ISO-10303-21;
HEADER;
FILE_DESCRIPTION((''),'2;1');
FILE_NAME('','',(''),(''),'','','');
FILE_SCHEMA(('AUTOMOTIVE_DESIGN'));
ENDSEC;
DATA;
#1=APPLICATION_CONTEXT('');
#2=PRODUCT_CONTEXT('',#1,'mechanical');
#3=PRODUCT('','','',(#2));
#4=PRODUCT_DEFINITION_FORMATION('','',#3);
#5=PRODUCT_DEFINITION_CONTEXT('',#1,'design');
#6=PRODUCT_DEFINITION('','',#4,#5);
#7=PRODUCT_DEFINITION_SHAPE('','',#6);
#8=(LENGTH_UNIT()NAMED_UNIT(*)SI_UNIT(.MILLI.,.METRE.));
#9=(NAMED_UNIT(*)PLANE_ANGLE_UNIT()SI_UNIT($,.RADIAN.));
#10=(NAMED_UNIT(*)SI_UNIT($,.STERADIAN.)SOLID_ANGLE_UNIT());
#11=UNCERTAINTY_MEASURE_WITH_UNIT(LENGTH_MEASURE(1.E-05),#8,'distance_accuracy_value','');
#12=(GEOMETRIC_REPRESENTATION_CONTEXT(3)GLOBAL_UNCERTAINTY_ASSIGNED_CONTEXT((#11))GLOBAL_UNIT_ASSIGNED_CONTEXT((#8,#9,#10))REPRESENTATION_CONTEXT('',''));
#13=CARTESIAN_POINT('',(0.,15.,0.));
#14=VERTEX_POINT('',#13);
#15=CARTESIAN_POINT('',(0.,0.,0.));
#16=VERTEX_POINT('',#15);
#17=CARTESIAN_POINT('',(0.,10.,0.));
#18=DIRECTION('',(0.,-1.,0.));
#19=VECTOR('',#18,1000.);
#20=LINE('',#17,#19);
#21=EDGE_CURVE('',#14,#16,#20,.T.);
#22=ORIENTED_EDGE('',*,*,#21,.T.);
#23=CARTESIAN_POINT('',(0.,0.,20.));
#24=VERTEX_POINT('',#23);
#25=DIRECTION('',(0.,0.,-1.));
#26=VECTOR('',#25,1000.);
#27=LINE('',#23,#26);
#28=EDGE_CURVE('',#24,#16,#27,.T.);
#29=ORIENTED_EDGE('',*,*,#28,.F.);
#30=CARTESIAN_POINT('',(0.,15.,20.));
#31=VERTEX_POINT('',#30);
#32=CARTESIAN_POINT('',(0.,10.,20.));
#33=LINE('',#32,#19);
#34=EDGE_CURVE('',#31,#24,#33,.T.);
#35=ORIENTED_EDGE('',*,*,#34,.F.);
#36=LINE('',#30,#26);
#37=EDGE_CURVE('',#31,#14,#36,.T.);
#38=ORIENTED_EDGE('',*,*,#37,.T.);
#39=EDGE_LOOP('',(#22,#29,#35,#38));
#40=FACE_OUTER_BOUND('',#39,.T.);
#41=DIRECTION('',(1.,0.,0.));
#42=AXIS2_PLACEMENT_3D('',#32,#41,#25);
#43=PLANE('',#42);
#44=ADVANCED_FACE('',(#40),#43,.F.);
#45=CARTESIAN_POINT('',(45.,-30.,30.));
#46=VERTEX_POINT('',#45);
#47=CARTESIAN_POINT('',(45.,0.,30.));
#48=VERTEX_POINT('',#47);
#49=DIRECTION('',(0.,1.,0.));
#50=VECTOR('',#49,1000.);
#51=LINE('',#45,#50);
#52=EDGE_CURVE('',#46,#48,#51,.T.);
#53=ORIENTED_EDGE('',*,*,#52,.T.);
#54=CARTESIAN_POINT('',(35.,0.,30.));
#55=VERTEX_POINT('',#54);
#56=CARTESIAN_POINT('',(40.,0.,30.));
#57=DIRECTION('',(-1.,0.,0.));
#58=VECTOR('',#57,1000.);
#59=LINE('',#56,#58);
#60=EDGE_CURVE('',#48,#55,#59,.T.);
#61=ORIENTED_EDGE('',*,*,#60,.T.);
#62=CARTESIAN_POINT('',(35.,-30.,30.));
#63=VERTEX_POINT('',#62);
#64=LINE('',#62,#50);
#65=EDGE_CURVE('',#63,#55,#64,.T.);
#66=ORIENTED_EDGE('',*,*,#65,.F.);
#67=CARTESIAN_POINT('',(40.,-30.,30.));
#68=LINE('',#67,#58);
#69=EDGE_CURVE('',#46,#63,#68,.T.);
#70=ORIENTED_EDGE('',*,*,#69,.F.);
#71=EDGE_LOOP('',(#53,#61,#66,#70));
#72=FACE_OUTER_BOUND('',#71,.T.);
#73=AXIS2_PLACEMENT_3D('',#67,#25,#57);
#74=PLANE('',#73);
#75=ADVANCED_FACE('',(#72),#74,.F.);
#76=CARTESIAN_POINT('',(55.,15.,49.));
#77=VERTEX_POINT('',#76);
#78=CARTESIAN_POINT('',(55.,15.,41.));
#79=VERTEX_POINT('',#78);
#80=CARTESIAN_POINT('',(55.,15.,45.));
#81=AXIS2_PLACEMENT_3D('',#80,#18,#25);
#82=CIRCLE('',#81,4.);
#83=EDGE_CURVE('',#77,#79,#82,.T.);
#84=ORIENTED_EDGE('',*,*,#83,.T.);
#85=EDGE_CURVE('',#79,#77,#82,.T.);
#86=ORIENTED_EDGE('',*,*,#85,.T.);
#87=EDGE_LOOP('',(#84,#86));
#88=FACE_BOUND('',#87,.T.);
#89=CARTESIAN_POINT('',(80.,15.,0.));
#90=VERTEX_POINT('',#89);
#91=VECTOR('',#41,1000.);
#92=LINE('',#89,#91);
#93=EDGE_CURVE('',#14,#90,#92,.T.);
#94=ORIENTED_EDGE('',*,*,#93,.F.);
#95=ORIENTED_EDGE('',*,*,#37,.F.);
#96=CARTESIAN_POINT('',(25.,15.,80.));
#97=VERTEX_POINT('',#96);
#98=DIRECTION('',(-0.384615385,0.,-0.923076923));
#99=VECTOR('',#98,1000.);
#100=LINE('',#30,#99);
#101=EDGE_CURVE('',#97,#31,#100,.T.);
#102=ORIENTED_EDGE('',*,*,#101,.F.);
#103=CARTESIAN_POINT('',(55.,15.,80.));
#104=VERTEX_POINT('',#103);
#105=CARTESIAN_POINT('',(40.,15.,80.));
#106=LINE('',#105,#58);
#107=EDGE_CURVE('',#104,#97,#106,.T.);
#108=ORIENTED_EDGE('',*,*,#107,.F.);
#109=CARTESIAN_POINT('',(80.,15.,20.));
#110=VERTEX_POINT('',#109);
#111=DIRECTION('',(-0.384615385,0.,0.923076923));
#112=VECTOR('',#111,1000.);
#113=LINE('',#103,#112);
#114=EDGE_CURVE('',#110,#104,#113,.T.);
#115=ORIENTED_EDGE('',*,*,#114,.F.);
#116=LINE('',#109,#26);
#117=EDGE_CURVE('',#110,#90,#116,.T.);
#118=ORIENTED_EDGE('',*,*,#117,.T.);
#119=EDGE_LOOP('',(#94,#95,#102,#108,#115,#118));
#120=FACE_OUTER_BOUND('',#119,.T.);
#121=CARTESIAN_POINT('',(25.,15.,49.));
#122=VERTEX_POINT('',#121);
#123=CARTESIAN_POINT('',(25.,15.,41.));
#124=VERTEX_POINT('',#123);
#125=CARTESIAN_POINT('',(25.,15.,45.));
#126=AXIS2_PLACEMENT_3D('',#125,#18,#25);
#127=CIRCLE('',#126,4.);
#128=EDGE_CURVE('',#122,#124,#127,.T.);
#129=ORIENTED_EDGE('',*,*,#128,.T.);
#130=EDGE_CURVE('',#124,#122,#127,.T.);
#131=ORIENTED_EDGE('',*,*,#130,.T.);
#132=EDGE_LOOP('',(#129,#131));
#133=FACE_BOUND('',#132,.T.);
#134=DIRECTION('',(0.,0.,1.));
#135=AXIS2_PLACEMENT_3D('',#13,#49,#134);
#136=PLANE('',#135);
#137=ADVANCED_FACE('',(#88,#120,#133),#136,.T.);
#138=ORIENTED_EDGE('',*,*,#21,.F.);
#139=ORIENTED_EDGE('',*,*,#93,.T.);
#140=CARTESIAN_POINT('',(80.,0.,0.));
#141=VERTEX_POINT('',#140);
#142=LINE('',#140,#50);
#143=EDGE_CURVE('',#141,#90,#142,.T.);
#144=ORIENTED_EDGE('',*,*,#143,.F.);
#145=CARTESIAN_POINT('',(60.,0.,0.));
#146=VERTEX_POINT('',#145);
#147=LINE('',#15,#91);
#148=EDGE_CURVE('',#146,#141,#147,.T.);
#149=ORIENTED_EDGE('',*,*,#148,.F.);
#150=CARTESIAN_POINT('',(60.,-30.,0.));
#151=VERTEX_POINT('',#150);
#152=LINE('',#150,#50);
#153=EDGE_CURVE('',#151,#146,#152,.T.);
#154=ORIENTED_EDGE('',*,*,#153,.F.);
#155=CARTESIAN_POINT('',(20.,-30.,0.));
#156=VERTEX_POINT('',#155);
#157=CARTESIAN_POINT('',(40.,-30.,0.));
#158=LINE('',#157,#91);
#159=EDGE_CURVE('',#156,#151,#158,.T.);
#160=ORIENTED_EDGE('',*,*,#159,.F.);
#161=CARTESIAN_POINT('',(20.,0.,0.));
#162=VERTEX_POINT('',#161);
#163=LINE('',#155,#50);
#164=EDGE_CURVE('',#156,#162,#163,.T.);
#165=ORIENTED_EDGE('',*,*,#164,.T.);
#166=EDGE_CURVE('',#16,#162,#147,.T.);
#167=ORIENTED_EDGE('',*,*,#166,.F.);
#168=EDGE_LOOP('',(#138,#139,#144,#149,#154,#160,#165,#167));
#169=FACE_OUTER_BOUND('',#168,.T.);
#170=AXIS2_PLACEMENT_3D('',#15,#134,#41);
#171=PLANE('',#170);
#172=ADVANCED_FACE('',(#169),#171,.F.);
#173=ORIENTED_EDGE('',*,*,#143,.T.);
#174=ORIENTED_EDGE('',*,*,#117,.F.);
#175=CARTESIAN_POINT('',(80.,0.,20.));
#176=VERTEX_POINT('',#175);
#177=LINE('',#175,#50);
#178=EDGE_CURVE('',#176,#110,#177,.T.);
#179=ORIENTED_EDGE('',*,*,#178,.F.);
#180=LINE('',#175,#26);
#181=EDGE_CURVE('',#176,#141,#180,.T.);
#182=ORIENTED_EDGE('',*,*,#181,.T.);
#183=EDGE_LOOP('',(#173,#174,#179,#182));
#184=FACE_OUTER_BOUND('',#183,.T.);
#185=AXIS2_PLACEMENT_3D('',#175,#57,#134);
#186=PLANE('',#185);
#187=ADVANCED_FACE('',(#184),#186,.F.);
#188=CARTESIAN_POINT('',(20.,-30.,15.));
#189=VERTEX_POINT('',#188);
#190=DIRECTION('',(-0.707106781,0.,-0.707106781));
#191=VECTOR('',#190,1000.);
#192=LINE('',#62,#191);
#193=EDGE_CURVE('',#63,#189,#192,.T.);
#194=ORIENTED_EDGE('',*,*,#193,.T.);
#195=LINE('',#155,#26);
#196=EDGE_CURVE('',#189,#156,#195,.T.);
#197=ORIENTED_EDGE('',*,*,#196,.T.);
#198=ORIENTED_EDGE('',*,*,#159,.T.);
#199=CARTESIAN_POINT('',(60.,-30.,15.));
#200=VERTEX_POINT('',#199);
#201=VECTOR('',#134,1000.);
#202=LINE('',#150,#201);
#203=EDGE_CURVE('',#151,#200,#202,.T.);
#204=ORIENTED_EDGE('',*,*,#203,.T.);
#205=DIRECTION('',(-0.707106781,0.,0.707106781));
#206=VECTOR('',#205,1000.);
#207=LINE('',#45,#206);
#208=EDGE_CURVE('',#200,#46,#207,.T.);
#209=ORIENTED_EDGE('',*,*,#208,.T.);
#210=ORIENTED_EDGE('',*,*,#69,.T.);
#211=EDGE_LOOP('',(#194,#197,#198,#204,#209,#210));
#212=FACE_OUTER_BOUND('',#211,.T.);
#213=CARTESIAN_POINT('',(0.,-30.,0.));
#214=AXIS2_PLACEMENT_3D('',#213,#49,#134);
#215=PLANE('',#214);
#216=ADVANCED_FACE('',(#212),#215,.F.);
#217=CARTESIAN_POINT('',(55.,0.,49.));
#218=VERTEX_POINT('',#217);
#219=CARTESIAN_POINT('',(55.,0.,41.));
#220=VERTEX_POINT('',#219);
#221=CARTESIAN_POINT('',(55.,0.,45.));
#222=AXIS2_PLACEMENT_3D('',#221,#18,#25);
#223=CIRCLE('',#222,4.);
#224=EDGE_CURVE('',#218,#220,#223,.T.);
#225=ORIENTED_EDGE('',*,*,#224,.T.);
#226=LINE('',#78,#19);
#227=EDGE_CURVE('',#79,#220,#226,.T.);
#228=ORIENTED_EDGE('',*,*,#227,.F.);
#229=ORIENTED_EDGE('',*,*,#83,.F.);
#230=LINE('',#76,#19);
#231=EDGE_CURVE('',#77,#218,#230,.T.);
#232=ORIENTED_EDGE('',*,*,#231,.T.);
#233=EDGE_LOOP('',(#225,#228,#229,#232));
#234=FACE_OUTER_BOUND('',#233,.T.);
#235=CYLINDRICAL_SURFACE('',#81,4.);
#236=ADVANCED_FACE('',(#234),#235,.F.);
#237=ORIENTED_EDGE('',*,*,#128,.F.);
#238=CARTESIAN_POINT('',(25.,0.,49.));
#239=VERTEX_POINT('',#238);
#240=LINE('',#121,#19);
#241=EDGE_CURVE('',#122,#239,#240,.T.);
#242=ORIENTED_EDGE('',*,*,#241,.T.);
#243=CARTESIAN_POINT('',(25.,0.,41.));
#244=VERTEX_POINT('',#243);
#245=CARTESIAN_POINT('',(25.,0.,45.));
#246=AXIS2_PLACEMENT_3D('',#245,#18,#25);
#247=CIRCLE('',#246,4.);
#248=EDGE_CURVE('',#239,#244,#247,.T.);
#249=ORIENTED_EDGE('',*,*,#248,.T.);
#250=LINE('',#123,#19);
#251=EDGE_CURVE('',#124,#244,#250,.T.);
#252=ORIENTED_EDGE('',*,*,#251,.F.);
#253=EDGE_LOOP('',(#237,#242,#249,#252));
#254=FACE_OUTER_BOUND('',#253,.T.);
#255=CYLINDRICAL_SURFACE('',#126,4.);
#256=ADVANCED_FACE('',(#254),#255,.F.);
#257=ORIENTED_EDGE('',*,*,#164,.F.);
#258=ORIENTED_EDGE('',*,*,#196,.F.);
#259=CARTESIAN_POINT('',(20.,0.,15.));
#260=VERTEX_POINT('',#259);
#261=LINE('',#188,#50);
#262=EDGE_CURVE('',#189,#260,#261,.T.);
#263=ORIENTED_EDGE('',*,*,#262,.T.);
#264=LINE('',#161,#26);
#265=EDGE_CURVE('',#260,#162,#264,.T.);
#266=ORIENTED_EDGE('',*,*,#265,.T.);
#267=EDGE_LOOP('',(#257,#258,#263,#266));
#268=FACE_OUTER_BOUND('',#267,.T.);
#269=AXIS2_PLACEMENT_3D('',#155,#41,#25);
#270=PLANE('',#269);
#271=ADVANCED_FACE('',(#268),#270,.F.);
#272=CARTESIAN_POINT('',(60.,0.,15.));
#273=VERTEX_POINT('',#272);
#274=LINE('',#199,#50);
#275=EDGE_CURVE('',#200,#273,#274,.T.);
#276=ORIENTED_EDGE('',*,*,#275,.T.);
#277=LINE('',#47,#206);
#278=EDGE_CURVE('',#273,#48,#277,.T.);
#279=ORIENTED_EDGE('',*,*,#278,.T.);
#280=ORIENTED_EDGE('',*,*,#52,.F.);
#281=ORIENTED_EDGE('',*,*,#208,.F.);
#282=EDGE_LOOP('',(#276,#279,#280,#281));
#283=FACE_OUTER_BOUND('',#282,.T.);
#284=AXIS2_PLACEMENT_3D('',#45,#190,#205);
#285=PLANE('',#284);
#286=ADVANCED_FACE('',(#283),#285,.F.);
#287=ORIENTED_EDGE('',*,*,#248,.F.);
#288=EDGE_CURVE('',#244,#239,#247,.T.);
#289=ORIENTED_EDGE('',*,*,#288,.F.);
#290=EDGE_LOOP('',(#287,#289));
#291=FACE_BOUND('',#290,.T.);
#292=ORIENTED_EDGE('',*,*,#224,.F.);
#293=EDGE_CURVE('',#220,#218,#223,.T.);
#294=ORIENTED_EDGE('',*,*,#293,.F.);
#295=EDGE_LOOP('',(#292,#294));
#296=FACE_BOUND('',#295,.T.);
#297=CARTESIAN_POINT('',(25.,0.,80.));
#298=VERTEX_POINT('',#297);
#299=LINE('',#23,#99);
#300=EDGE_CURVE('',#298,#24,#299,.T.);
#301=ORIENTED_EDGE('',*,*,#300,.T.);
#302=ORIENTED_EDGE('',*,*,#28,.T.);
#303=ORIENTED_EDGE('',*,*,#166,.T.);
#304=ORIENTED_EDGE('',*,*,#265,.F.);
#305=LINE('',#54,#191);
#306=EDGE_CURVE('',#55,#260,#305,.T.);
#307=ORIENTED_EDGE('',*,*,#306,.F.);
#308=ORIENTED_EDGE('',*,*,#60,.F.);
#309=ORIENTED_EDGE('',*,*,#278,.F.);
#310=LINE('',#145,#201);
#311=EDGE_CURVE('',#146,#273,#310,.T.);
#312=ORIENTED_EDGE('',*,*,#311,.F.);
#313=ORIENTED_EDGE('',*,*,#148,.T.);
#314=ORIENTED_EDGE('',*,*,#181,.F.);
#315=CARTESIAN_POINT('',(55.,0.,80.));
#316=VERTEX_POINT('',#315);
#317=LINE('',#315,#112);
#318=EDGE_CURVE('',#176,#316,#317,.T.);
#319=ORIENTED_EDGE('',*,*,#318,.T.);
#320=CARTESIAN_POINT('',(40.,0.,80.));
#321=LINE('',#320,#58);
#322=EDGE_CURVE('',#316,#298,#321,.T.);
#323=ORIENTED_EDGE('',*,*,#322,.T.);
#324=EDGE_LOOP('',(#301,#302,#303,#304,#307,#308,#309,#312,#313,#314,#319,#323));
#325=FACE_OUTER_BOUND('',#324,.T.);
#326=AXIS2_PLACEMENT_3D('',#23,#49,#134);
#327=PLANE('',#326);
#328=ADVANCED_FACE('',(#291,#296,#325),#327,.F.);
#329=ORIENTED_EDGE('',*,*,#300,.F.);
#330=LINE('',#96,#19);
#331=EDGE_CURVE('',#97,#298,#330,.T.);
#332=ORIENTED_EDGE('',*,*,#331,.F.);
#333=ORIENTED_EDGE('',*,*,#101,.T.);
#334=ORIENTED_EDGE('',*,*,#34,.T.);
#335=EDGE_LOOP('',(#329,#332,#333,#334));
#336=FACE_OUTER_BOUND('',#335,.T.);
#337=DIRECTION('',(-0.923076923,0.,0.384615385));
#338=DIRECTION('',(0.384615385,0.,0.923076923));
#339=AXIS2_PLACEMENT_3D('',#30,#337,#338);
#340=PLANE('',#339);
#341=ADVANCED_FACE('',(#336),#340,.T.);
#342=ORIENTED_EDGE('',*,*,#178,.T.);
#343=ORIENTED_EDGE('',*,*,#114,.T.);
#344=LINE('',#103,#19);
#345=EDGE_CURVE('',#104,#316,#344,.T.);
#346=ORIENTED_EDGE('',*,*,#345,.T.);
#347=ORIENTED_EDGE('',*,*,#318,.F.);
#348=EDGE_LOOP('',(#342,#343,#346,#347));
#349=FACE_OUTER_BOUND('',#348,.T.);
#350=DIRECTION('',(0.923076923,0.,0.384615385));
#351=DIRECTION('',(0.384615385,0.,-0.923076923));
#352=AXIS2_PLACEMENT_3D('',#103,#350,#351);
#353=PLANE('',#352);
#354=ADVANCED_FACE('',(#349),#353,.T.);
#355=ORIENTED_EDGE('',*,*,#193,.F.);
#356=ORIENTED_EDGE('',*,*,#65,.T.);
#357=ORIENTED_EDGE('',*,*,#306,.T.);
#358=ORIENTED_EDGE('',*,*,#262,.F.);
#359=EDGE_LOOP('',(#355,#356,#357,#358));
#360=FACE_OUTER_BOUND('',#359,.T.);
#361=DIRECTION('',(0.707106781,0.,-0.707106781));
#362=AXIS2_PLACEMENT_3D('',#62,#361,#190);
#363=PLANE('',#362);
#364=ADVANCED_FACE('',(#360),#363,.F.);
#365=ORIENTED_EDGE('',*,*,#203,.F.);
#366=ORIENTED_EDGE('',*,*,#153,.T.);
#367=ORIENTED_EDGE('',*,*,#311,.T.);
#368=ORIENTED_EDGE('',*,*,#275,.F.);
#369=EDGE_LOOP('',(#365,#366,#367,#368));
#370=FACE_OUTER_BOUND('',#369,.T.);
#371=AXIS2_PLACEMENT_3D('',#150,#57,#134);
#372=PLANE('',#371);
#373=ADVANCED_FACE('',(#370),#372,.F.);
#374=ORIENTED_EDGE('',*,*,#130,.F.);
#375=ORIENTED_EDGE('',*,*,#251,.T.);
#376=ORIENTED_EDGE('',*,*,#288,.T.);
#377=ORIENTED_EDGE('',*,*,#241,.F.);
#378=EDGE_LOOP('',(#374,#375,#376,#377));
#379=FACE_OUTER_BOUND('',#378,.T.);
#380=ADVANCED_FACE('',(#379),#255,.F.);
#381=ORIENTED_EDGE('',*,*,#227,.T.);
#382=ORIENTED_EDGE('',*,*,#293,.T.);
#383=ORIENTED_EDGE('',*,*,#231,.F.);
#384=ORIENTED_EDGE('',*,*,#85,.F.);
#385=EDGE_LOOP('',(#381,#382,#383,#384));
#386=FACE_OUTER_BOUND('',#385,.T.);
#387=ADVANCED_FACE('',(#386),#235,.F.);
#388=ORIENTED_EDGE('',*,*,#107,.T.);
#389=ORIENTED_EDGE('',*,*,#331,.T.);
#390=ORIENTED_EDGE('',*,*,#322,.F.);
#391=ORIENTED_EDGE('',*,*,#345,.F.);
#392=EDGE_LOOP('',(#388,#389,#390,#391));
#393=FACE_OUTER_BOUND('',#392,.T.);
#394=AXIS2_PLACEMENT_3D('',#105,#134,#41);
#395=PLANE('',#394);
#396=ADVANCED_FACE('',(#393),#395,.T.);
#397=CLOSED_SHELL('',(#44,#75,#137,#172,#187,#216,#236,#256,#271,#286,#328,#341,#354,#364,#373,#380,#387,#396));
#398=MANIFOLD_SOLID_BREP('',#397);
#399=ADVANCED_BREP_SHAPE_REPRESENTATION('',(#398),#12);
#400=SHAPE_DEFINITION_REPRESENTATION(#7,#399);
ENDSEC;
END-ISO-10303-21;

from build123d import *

# Parameters (mm, degrees)
BASE_PLATE_SKETCH_W      = 80
BASE_PLATE_SKETCH_H      = 10
BASE_PLATE_DEPTH         = 20
PENTAGONAL_BOSS_DEPTH    = 15
FOUR_SIDED_BOSS_SKETCH_W = 80
FOUR_SIDED_BOSS_SKETCH_H = 5
FOUR_SIDED_BOSS_DEPTH    = 20
OCTAGONAL_BOSS_DEPTH     = 30
HOLES_2X_8_SKETCH_R      = 4
HOLES_2X_8_DEPTH         = 15


with BuildPart() as part:
    # Base Plate Sketch → Base Plate (new body)
    with BuildSketch(Plane.XY):
        with Locations((40, 5)):
            Rectangle(BASE_PLATE_SKETCH_W, BASE_PLATE_SKETCH_H)
    extrude(amount=BASE_PLATE_DEPTH)

    # Pentagonal Boss Sketch → Pentagonal Boss (add)
    with BuildSketch(Plane.XZ):
        Polygon((40, 80), (25, 80), (0, 20), (80, 20), (55, 80), align=None)
    extrude(amount=-PENTAGONAL_BOSS_DEPTH)

    # Four-Sided Boss Sketch → Four-Sided Boss (add)
    with BuildSketch(Plane(origin=(0, 0, 0), x_dir=(-1, 0, 0), z_dir=(0, 0, -1))):
        with Locations((-40, 12.5)):
            Rectangle(FOUR_SIDED_BOSS_SKETCH_W, FOUR_SIDED_BOSS_SKETCH_H)
    extrude(amount=-FOUR_SIDED_BOSS_DEPTH)

    # Octagonal Boss Sketch → Octagonal Boss (add)
    with BuildSketch(Plane.XZ):
        Polygon((40, 0), (60, 0), (60, 15), (45, 30), (40, 30), (35, 30), (20, 15), (20, 0), align=None)
    extrude(amount=OCTAGONAL_BOSS_DEPTH)

    # Holes 2xØ8 Sketch → Holes 2xØ8 (cut)
    with BuildSketch(Plane.XZ):
        with Locations(Location((25, 45, 0), (0, 0, 270))):
            Circle(HOLES_2X_8_SKETCH_R)
        with Locations(Location((55, 45, 0), (0, 0, 270))):
            Circle(HOLES_2X_8_SKETCH_R)
    extrude(amount=-HOLES_2X_8_DEPTH, mode=Mode.SUBTRACT)


solid = part.part
